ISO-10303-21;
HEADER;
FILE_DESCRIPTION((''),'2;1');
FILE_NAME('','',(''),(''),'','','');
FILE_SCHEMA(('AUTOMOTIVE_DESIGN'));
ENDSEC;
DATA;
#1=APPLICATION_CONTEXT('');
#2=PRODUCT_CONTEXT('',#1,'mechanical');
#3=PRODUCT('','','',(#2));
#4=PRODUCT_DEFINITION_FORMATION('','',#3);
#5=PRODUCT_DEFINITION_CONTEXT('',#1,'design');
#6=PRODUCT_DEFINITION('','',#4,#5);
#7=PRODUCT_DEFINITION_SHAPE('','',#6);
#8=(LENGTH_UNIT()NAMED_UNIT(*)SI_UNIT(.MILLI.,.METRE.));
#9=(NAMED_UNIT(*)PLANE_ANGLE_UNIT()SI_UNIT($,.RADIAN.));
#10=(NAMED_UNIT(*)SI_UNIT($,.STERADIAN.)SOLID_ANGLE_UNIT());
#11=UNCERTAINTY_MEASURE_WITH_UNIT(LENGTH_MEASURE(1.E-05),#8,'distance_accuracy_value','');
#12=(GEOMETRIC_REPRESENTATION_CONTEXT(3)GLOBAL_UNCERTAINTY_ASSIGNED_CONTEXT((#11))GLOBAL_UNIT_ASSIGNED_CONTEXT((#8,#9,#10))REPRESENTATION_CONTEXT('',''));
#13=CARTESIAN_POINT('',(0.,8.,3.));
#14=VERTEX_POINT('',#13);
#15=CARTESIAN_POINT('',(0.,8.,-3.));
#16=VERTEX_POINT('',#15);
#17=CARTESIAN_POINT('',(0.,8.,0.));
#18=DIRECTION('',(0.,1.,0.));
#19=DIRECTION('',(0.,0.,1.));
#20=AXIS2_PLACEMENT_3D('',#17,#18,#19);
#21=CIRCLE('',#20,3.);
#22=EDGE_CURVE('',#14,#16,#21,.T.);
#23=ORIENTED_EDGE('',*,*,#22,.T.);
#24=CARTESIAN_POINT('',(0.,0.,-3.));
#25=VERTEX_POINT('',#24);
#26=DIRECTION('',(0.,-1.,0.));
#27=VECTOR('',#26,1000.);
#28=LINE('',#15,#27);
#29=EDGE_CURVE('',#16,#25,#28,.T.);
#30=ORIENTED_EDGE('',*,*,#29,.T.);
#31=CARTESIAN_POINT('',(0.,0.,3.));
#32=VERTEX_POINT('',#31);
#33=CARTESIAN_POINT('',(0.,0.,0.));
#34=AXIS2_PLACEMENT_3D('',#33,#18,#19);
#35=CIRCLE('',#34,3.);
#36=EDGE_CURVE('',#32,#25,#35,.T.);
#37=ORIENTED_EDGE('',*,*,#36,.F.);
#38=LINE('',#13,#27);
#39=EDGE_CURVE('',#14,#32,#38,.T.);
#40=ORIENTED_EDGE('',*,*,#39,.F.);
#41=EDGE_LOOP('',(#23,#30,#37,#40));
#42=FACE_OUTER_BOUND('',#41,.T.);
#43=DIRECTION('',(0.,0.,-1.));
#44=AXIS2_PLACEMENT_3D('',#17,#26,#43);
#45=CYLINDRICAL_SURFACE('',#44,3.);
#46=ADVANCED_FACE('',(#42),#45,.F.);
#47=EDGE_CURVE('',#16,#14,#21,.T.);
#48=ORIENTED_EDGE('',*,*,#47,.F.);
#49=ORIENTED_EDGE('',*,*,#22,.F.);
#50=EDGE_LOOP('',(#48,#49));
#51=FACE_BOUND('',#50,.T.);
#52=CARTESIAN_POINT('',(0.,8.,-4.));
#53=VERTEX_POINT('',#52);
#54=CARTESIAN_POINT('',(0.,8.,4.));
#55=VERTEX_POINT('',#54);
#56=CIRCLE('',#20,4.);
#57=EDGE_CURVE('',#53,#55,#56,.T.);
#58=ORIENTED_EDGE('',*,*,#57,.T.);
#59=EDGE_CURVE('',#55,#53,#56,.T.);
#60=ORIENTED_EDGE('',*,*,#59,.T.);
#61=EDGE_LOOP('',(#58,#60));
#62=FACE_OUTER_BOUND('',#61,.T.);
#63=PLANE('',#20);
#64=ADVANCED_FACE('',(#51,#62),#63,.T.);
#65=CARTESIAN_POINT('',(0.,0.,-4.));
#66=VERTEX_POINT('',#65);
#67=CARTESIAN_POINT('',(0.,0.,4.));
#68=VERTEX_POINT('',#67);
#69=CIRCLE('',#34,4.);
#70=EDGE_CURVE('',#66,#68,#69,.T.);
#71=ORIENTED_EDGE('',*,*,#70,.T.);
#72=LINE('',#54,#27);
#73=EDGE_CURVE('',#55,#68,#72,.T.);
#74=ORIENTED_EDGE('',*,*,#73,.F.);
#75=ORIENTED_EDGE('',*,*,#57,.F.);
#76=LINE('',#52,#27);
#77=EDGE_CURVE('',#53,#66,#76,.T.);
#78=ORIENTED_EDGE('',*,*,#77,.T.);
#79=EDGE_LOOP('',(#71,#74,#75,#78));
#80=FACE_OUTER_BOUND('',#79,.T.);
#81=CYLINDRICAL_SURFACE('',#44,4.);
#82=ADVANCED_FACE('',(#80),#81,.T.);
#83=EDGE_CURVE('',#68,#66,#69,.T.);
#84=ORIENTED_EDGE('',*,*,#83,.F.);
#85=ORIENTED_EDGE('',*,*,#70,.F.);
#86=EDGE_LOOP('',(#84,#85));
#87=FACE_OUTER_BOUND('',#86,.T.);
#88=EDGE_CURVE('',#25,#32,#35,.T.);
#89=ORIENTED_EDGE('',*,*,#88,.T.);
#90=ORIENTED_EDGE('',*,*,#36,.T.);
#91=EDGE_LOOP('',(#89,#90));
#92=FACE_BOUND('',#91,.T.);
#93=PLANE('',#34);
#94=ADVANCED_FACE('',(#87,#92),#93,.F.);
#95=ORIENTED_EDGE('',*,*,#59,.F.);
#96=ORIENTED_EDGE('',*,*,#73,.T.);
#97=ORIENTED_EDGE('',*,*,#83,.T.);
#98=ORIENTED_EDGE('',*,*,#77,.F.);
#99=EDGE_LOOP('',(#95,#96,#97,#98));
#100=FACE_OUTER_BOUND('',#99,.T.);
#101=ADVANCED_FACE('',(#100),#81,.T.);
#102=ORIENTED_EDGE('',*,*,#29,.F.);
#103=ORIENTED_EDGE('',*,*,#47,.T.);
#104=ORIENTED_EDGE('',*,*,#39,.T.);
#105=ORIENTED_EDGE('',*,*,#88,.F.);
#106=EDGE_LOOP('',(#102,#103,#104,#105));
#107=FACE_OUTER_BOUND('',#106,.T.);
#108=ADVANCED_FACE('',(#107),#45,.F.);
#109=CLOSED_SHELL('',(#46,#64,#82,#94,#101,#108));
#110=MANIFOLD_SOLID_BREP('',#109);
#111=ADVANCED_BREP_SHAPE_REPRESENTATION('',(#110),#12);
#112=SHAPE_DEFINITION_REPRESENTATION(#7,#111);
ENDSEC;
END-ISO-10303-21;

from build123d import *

# Parameters (mm, degrees)
SKETCH_1_R      = 4
SKETCH_1_R_2    = 3
EXTRUDE_1_DEPTH = 8


with BuildPart() as part:
    # 草图1 → 凸台-拉伸1 (new body)
    with BuildSketch(Plane(origin=(0, 0, 0), x_dir=(1, 0, 0), z_dir=(0, 1, 0))):
        with Locations(Location((0, 0, 0), (0, 0, 270))):
            Circle(SKETCH_1_R)
        with Locations(Location((0, 0, 0), (0, 0, 270))):
            Circle(SKETCH_1_R_2, mode=Mode.SUBTRACT)
    extrude(amount=EXTRUDE_1_DEPTH)


solid = part.part
